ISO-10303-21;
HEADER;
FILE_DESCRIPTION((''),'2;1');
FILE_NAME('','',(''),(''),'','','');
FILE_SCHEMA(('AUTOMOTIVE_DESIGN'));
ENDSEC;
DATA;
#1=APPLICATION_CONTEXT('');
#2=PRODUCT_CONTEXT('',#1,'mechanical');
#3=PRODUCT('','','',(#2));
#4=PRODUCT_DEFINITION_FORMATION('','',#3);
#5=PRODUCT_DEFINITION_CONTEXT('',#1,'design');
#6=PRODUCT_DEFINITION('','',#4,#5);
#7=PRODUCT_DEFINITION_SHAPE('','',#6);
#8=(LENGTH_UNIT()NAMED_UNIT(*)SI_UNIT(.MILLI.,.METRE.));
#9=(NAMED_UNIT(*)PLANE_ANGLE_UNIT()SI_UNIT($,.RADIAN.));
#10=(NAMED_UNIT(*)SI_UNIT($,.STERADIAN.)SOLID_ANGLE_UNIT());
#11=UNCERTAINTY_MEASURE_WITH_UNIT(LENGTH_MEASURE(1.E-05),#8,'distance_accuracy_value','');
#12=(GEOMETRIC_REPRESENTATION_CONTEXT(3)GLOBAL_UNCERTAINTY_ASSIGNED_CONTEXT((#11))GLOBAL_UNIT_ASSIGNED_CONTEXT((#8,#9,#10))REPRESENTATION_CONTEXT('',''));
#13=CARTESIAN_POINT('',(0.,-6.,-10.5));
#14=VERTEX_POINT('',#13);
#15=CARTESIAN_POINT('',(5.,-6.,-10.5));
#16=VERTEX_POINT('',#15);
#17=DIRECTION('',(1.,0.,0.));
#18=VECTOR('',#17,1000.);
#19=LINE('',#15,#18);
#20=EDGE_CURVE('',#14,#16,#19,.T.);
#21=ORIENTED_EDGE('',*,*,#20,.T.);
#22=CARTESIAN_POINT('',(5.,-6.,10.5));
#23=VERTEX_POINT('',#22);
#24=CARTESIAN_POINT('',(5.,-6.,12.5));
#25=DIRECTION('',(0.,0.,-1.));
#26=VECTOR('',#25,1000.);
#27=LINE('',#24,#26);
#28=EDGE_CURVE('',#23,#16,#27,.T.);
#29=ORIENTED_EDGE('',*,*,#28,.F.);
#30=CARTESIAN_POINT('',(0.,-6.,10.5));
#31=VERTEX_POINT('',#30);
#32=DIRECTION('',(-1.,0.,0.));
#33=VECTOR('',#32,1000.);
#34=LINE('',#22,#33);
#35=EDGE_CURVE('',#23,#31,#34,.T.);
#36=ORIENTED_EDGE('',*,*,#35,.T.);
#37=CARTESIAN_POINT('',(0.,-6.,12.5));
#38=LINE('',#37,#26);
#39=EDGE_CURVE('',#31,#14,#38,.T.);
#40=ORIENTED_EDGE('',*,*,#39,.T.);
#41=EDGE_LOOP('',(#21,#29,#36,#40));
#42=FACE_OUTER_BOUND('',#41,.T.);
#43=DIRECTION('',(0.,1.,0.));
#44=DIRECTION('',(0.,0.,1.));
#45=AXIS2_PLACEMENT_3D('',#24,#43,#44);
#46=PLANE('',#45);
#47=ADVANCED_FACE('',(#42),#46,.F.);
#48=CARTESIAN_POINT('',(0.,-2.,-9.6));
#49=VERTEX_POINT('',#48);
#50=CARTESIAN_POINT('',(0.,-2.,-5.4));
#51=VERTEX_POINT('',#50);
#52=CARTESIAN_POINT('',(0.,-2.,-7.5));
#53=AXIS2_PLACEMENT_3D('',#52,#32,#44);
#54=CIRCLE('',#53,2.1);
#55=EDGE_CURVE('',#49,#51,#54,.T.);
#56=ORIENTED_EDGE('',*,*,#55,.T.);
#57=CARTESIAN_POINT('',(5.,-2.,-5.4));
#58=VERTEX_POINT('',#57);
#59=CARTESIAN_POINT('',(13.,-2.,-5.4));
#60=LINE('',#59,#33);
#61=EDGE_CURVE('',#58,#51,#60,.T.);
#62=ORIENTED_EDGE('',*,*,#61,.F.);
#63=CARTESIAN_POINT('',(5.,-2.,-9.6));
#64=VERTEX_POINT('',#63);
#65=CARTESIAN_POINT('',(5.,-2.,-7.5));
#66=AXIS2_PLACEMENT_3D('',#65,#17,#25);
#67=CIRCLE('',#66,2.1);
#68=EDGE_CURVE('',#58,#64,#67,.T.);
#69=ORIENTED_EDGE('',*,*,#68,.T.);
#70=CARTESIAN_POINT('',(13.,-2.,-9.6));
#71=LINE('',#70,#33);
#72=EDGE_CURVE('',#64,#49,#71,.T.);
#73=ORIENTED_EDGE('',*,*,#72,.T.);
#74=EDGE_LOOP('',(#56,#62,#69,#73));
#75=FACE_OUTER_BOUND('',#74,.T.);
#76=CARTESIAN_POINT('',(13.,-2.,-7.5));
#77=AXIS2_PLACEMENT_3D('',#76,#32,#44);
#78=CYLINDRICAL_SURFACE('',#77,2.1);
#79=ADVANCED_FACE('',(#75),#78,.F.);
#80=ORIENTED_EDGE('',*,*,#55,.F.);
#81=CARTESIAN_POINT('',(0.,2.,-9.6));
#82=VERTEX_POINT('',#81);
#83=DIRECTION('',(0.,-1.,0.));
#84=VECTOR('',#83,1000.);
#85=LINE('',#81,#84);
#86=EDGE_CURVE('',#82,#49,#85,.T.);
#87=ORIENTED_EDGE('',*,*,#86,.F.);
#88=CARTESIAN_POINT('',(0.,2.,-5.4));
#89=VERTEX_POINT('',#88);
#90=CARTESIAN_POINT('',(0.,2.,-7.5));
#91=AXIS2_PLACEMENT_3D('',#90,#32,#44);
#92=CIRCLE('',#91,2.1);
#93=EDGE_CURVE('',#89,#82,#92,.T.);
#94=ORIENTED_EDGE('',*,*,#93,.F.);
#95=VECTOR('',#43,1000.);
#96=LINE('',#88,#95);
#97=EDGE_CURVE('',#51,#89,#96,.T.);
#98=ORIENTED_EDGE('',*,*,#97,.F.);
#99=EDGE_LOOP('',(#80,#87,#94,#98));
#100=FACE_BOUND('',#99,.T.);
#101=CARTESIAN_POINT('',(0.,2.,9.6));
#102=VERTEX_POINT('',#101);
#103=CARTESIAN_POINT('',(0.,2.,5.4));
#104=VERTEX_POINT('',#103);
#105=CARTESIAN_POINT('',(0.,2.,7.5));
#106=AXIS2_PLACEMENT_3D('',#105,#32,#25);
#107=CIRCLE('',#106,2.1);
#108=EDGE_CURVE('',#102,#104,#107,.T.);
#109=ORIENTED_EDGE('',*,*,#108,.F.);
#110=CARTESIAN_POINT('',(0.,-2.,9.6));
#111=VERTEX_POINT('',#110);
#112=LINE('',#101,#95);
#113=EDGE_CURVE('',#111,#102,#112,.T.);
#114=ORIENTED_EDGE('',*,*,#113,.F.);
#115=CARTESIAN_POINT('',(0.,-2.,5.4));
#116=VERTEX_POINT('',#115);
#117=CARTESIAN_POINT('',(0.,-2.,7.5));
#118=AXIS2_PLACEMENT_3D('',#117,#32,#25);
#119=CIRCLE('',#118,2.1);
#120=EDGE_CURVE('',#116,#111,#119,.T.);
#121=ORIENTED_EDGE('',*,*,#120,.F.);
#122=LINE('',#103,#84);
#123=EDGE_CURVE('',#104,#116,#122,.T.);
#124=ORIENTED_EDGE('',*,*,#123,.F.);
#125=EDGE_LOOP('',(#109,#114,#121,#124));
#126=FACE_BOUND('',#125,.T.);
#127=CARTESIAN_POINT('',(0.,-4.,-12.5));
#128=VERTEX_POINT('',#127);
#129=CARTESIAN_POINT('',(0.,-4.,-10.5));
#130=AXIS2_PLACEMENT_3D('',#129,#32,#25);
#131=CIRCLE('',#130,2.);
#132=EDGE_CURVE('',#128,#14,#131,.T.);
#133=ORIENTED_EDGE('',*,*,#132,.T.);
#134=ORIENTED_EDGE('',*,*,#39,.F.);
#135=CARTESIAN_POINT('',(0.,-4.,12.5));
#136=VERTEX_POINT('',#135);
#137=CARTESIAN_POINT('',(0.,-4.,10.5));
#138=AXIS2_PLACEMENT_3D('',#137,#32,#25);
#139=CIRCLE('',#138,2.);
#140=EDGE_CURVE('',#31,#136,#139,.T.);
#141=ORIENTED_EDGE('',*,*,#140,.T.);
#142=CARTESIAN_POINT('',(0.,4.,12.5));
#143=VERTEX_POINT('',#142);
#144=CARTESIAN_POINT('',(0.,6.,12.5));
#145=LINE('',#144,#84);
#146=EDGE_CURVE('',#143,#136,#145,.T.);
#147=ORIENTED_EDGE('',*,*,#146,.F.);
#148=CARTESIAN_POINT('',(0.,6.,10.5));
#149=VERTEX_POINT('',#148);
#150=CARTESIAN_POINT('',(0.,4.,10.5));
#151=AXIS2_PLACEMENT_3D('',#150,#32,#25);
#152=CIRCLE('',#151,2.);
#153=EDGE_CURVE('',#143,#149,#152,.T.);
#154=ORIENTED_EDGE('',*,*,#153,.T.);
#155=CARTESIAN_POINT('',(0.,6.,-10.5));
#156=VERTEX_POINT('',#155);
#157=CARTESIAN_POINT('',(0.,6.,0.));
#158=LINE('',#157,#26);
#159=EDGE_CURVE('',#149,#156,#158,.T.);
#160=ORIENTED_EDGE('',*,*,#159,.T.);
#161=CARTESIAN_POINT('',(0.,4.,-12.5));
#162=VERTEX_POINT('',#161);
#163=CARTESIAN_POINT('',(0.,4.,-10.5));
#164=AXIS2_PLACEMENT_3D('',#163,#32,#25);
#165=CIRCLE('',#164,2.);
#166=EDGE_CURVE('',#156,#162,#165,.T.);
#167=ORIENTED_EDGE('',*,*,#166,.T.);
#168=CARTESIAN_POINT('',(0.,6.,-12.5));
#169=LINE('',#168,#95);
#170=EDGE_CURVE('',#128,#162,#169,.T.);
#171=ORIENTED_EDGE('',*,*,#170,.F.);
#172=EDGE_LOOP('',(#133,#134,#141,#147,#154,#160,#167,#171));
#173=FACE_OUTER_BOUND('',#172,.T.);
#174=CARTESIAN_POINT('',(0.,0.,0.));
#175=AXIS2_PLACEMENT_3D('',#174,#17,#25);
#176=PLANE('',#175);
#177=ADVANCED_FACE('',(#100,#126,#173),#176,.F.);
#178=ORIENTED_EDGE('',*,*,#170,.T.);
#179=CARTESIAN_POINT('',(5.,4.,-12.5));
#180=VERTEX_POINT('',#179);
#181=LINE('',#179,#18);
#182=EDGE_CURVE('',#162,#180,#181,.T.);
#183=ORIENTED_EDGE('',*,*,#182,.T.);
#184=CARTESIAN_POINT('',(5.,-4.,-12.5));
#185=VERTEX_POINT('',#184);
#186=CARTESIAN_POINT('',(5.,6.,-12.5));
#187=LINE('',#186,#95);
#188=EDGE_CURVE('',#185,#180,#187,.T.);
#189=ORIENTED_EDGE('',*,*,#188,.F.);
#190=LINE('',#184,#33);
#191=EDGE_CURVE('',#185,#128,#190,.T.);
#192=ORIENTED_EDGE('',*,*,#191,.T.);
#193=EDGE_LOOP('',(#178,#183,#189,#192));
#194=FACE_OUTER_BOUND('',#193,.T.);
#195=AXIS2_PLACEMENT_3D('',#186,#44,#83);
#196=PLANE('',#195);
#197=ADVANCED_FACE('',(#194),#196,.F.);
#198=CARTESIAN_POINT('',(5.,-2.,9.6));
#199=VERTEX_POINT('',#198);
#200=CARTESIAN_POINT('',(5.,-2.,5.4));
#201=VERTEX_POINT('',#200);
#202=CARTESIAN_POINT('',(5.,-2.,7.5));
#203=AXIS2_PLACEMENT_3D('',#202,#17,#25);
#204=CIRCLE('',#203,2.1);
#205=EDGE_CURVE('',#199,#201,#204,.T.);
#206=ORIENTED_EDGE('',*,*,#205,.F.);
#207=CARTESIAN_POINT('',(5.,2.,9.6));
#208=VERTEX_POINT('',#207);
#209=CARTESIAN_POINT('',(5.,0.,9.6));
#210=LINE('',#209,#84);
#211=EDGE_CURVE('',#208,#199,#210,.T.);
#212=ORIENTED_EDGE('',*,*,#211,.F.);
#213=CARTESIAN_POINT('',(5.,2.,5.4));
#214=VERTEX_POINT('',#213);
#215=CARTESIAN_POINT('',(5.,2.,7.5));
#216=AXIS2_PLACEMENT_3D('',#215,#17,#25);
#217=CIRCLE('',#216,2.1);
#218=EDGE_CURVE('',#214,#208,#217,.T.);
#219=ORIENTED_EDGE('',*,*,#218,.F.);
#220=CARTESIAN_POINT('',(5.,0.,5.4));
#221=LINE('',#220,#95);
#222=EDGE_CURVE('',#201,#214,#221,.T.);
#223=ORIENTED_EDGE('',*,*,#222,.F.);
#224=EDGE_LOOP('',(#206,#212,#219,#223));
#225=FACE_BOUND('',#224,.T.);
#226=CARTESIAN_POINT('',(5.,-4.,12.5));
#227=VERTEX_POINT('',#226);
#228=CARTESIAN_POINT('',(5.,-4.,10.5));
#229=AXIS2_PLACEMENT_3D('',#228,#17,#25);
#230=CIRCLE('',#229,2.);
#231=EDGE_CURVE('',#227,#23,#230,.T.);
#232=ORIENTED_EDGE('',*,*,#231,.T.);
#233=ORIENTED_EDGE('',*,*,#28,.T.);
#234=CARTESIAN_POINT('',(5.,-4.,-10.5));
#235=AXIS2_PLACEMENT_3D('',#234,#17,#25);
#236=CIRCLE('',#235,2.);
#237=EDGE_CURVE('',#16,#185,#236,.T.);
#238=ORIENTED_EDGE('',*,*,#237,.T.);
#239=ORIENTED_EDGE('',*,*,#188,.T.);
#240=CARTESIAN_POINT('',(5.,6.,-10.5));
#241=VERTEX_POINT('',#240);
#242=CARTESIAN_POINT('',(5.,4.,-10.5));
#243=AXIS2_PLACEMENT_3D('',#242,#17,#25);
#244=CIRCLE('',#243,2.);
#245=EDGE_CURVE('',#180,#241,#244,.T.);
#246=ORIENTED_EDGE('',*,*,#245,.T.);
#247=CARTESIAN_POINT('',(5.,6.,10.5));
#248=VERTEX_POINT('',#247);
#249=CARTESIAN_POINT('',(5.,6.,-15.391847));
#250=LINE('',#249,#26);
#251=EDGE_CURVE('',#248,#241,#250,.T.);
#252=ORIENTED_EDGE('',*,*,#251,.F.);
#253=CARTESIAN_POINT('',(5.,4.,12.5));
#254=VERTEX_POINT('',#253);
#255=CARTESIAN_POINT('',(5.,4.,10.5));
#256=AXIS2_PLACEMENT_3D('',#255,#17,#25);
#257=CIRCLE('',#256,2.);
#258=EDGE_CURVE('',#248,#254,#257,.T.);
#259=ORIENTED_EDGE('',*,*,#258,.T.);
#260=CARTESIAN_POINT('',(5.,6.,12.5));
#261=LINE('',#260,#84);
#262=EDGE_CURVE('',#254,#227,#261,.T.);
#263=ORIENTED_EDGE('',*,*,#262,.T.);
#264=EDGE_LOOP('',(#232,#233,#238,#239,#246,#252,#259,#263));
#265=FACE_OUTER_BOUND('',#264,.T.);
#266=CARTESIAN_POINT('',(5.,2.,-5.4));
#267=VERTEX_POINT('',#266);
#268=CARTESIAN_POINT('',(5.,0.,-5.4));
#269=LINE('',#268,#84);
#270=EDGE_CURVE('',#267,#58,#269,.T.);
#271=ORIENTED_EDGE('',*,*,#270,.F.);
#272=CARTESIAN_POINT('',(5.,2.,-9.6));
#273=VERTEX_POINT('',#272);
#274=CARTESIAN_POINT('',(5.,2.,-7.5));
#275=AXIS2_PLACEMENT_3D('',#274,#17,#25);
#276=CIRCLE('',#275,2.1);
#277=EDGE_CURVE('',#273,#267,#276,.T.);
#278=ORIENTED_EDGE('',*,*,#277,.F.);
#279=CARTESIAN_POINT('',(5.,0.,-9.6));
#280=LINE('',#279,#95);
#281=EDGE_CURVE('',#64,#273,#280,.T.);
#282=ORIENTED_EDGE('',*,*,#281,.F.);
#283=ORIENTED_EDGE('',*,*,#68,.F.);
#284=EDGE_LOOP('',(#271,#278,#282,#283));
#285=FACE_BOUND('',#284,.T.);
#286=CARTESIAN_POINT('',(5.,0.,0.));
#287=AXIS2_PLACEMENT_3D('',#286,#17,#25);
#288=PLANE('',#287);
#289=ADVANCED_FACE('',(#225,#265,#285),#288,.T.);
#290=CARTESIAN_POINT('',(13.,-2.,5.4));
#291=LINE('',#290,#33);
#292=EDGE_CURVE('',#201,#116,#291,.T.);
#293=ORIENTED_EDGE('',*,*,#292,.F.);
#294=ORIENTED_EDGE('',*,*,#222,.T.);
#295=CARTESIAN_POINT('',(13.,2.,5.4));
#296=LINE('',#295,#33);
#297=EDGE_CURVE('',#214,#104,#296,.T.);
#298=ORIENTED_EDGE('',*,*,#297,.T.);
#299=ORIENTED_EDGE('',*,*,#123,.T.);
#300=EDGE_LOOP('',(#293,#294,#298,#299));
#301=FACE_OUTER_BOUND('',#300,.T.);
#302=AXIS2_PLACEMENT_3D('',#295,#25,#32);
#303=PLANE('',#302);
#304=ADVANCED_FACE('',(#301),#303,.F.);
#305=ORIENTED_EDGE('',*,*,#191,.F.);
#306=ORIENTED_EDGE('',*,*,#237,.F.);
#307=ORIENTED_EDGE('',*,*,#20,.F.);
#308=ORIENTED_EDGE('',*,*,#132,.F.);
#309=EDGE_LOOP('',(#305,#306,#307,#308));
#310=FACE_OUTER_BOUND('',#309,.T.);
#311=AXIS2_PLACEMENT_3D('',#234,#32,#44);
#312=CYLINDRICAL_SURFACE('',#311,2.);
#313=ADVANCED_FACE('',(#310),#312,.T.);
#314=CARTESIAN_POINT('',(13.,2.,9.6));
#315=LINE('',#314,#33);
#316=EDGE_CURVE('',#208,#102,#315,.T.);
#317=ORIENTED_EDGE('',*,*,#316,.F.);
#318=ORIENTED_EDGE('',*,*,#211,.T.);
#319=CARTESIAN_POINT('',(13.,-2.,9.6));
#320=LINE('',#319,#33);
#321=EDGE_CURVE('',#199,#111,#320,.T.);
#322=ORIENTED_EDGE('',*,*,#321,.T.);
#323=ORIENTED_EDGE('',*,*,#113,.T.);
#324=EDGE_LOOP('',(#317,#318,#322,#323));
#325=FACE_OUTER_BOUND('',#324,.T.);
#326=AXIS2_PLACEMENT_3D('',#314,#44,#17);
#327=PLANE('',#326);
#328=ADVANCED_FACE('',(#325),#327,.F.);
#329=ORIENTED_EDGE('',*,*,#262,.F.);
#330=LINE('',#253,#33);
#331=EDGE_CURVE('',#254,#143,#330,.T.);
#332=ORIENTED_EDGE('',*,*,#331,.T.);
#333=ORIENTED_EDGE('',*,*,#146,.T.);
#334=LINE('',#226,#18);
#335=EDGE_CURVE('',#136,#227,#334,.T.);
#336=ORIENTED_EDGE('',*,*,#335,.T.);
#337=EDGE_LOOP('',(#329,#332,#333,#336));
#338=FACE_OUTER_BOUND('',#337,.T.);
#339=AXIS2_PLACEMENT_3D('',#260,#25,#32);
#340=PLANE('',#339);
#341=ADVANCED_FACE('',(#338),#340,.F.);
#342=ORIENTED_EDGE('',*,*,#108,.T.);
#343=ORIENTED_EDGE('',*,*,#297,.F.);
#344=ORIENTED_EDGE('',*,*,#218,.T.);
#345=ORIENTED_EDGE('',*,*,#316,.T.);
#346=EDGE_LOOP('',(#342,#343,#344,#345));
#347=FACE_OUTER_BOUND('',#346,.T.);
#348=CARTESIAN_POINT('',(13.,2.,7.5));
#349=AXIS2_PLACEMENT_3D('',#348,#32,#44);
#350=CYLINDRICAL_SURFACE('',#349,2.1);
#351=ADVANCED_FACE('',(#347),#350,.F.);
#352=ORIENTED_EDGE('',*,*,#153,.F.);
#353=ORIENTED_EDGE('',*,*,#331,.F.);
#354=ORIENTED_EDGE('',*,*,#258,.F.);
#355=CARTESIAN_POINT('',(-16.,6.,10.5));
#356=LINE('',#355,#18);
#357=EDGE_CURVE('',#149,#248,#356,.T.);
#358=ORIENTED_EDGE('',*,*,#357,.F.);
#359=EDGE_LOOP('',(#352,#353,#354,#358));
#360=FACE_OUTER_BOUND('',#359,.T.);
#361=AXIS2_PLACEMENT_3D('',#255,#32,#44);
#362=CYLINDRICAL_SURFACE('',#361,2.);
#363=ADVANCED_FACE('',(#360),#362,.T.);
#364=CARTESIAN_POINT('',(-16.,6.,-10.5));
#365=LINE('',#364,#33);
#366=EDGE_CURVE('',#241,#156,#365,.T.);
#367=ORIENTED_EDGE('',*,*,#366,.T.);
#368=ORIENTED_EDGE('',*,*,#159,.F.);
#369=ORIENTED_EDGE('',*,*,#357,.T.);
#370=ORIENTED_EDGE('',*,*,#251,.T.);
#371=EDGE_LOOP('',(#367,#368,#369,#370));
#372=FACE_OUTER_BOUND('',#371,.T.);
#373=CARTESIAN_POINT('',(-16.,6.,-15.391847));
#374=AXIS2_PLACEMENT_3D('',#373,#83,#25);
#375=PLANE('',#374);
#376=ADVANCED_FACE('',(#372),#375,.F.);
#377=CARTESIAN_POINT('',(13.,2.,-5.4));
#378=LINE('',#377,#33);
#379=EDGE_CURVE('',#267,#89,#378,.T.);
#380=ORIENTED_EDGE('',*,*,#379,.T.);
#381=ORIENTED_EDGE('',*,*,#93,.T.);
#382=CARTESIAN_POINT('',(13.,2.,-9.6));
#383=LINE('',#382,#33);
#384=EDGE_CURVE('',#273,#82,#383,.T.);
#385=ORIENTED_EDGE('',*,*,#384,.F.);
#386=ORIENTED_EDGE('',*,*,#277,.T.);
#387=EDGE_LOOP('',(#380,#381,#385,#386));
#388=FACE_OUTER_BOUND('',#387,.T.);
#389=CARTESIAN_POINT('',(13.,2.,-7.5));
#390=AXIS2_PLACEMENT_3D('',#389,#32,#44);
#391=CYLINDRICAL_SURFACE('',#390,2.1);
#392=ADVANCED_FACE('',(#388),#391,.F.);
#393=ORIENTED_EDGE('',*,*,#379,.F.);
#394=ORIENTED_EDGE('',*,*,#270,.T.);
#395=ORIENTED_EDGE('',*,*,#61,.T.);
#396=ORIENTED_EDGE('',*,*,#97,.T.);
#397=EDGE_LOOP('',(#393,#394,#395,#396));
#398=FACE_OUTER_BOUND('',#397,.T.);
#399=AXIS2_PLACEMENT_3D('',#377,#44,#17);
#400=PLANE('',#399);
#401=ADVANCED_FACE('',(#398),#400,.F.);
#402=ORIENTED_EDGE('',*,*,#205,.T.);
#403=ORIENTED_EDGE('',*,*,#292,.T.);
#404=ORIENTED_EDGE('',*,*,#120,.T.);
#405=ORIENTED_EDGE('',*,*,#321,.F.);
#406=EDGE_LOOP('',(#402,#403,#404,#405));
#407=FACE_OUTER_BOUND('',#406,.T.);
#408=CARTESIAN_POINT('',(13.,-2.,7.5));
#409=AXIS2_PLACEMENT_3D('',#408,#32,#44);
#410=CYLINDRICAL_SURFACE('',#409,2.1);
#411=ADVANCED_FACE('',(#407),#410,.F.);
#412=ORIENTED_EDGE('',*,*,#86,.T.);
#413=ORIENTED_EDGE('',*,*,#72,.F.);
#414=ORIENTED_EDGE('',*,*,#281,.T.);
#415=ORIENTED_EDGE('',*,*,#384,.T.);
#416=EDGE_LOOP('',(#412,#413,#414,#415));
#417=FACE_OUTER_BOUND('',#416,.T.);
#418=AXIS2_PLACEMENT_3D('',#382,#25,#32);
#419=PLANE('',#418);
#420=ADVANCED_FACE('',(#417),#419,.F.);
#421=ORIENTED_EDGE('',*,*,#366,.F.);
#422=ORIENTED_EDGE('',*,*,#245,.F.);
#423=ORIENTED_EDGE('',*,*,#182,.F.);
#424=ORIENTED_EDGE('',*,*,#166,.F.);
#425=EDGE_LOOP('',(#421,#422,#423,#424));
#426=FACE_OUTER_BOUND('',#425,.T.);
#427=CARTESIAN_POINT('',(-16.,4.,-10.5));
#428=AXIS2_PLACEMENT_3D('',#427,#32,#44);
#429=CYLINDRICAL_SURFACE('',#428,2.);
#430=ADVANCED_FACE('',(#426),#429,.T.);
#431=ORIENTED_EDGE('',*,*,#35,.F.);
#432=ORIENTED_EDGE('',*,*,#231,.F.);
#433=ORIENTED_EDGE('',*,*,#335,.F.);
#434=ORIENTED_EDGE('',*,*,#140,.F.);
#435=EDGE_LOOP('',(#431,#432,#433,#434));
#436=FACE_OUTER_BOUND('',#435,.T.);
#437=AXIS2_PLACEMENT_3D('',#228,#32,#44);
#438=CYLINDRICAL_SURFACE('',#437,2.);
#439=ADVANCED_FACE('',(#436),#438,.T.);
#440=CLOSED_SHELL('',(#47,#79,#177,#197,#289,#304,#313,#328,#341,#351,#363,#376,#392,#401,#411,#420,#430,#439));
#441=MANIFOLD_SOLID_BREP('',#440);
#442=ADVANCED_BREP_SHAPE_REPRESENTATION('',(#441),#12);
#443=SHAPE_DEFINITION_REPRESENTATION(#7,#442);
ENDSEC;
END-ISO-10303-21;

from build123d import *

# Parameters (mm, degrees)
EXTRUDE_1_DEPTH             = 5
EXTRUDE_2_DEPTH             = 5
FILLET_1_R                  = 2
CUT_EXTRUDE_1_DEPTH         = 13
FILLET_2_R                  = 2
HOLE_WIZARD_4_3_4_3_1_D     = 4.3
HOLE_WIZARD_4_3_4_3_1_DEPTH = 10.1
HOLE_WIZARD_4_3_4_3_1_TIP   = 1.291850331
SKETCH_7_W                  = 24.449376322
SKETCH_7_H                  = 27.885292322
CUT_EXTRUDE_2_DEPTH         = 10
CUT_EXTRUDE_3_DEPTH         = 10
FILLET_3_R                  = 5
SKETCH_9_W                  = 36.796643843
SKETCH_9_H                  = 32.156214513
CUT_EXTRUDE_4_DEPTH         = 21
FILLET_4_R                  = 2


with BuildPart() as part:
    # 草图1 → 凸台-拉伸1 (new body)
    with BuildSketch(Plane(origin=(0, 0, 0), x_dir=(0, 0, -1), z_dir=(1, 0, 0))):
        Polygon((-12.5, 6), (-6, 6), (-6, 61), (6, 61), (6, 6), (12.5, 6), (12.5, -6), (-12.5, -6), align=None)
    extrude(amount=EXTRUDE_1_DEPTH)

    # 草图2 → 凸台-拉伸2 (add)
    with BuildSketch(Plane.ZY):
        Polygon((-6, 61), (-12.5, 6), (12.5, 6), (6, 61), align=None)
    extrude(amount=-EXTRUDE_2_DEPTH)

    # 圆角1
    fillet_1_edges = [part.edges().sort_by_distance(p)[0] for p in [
        (2.5, 61, 6),
        (2.5, 61, -6),
    ]]
    fillet(fillet_1_edges, radius=FILLET_1_R)

    # 草图3 → 切除-拉伸1 (cut)
    with BuildSketch(Plane.ZY):
        with BuildLine():
            Line((-5.4, 2), (-5.4, -2))
            ThreePointArc((-5.4, -2), (-7.5, -4.1), (-9.6, -2))
            Line((-9.6, -2), (-9.6, 2))
            ThreePointArc((-9.6, 2), (-7.5, 4.1), (-5.4, 2))
        make_face()
        with BuildLine():
            Line((5.4, 2), (5.4, -2))
            ThreePointArc((5.4, -2), (7.5, -4.1), (9.6, -2))
            Line((9.6, -2), (9.6, 2))
            ThreePointArc((9.6, 2), (7.5, 4.1), (5.4, 2))
        make_face()
    extrude(amount=-CUT_EXTRUDE_1_DEPTH, mode=Mode.SUBTRACT)

    # 圆角2
    fillet_2_edges = [part.edges().sort_by_distance(p)[0] for p in [
        (2.5, -6, -12.5),
        (2.5, -6, 12.5),
    ]]
    fillet(fillet_2_edges, radius=FILLET_2_R)

    # Ø4.3 (4.3) 直径孔1
    with Locations(Plane.ZY):
        with Locations((0, 56), (0, 41)):
            Hole(HOLE_WIZARD_4_3_4_3_1_D / 2, depth=HOLE_WIZARD_4_3_4_3_1_DEPTH)
            with Locations((0, 0, -(HOLE_WIZARD_4_3_4_3_1_DEPTH + HOLE_WIZARD_4_3_4_3_1_TIP / 2))):  # 118° drill point
                Cone(0, HOLE_WIZARD_4_3_4_3_1_D / 2, HOLE_WIZARD_4_3_4_3_1_TIP, mode=Mode.SUBTRACT)

    # 草图7 → 切除-拉伸2 (cut)
    with BuildSketch(Plane(origin=(5, 0, 0), x_dir=(0, 0, -1), z_dir=(1, 0, 0))):
        with Locations((-1.251346032, 49.942646161)):
            Rectangle(SKETCH_7_W, SKETCH_7_H)
    extrude(amount=-CUT_EXTRUDE_2_DEPTH, mode=Mode.SUBTRACT)

    # 草图8 → 切除-拉伸3 (cut)
    with BuildSketch(Plane.ZY):
        with BuildLine():
            Line((-1, 33.75), (1, 33.75))
            ThreePointArc((1, 33.75), (3.25, 31.5), (1, 29.25))
            Line((1, 29.25), (-1, 29.25))
            ThreePointArc((-1, 29.25), (-3.25, 31.5), (-1, 33.75))
        make_face()
    extrude(amount=-CUT_EXTRUDE_3_DEPTH, mode=Mode.SUBTRACT)

    # 圆角3
    fillet_3_edges = [part.edges().sort_by_distance(p)[0] for p in [
        (2.5, 36, 8.954545455),
        (2.5, 36, -8.954545455),
    ]]
    fillet(fillet_3_edges, radius=FILLET_3_R)

    # 草图9 → 切除-拉伸4 (cut)
    with BuildSketch(Plane(origin=(5, 0, 0), x_dir=(0, 0, -1), z_dir=(1, 0, 0))):
        with Locations((-3.006475341, 22.078107257)):
            Rectangle(SKETCH_9_W, SKETCH_9_H)
    extrude(amount=-CUT_EXTRUDE_4_DEPTH, mode=Mode.SUBTRACT)

    # 圆角4
    fillet_4_edges = [part.edges().sort_by_distance(p)[0] for p in [
        (2.5, 6, 12.5),
        (2.5, 6, -12.5),
    ]]
    fillet(fillet_4_edges, radius=FILLET_4_R)


solid = part.part
